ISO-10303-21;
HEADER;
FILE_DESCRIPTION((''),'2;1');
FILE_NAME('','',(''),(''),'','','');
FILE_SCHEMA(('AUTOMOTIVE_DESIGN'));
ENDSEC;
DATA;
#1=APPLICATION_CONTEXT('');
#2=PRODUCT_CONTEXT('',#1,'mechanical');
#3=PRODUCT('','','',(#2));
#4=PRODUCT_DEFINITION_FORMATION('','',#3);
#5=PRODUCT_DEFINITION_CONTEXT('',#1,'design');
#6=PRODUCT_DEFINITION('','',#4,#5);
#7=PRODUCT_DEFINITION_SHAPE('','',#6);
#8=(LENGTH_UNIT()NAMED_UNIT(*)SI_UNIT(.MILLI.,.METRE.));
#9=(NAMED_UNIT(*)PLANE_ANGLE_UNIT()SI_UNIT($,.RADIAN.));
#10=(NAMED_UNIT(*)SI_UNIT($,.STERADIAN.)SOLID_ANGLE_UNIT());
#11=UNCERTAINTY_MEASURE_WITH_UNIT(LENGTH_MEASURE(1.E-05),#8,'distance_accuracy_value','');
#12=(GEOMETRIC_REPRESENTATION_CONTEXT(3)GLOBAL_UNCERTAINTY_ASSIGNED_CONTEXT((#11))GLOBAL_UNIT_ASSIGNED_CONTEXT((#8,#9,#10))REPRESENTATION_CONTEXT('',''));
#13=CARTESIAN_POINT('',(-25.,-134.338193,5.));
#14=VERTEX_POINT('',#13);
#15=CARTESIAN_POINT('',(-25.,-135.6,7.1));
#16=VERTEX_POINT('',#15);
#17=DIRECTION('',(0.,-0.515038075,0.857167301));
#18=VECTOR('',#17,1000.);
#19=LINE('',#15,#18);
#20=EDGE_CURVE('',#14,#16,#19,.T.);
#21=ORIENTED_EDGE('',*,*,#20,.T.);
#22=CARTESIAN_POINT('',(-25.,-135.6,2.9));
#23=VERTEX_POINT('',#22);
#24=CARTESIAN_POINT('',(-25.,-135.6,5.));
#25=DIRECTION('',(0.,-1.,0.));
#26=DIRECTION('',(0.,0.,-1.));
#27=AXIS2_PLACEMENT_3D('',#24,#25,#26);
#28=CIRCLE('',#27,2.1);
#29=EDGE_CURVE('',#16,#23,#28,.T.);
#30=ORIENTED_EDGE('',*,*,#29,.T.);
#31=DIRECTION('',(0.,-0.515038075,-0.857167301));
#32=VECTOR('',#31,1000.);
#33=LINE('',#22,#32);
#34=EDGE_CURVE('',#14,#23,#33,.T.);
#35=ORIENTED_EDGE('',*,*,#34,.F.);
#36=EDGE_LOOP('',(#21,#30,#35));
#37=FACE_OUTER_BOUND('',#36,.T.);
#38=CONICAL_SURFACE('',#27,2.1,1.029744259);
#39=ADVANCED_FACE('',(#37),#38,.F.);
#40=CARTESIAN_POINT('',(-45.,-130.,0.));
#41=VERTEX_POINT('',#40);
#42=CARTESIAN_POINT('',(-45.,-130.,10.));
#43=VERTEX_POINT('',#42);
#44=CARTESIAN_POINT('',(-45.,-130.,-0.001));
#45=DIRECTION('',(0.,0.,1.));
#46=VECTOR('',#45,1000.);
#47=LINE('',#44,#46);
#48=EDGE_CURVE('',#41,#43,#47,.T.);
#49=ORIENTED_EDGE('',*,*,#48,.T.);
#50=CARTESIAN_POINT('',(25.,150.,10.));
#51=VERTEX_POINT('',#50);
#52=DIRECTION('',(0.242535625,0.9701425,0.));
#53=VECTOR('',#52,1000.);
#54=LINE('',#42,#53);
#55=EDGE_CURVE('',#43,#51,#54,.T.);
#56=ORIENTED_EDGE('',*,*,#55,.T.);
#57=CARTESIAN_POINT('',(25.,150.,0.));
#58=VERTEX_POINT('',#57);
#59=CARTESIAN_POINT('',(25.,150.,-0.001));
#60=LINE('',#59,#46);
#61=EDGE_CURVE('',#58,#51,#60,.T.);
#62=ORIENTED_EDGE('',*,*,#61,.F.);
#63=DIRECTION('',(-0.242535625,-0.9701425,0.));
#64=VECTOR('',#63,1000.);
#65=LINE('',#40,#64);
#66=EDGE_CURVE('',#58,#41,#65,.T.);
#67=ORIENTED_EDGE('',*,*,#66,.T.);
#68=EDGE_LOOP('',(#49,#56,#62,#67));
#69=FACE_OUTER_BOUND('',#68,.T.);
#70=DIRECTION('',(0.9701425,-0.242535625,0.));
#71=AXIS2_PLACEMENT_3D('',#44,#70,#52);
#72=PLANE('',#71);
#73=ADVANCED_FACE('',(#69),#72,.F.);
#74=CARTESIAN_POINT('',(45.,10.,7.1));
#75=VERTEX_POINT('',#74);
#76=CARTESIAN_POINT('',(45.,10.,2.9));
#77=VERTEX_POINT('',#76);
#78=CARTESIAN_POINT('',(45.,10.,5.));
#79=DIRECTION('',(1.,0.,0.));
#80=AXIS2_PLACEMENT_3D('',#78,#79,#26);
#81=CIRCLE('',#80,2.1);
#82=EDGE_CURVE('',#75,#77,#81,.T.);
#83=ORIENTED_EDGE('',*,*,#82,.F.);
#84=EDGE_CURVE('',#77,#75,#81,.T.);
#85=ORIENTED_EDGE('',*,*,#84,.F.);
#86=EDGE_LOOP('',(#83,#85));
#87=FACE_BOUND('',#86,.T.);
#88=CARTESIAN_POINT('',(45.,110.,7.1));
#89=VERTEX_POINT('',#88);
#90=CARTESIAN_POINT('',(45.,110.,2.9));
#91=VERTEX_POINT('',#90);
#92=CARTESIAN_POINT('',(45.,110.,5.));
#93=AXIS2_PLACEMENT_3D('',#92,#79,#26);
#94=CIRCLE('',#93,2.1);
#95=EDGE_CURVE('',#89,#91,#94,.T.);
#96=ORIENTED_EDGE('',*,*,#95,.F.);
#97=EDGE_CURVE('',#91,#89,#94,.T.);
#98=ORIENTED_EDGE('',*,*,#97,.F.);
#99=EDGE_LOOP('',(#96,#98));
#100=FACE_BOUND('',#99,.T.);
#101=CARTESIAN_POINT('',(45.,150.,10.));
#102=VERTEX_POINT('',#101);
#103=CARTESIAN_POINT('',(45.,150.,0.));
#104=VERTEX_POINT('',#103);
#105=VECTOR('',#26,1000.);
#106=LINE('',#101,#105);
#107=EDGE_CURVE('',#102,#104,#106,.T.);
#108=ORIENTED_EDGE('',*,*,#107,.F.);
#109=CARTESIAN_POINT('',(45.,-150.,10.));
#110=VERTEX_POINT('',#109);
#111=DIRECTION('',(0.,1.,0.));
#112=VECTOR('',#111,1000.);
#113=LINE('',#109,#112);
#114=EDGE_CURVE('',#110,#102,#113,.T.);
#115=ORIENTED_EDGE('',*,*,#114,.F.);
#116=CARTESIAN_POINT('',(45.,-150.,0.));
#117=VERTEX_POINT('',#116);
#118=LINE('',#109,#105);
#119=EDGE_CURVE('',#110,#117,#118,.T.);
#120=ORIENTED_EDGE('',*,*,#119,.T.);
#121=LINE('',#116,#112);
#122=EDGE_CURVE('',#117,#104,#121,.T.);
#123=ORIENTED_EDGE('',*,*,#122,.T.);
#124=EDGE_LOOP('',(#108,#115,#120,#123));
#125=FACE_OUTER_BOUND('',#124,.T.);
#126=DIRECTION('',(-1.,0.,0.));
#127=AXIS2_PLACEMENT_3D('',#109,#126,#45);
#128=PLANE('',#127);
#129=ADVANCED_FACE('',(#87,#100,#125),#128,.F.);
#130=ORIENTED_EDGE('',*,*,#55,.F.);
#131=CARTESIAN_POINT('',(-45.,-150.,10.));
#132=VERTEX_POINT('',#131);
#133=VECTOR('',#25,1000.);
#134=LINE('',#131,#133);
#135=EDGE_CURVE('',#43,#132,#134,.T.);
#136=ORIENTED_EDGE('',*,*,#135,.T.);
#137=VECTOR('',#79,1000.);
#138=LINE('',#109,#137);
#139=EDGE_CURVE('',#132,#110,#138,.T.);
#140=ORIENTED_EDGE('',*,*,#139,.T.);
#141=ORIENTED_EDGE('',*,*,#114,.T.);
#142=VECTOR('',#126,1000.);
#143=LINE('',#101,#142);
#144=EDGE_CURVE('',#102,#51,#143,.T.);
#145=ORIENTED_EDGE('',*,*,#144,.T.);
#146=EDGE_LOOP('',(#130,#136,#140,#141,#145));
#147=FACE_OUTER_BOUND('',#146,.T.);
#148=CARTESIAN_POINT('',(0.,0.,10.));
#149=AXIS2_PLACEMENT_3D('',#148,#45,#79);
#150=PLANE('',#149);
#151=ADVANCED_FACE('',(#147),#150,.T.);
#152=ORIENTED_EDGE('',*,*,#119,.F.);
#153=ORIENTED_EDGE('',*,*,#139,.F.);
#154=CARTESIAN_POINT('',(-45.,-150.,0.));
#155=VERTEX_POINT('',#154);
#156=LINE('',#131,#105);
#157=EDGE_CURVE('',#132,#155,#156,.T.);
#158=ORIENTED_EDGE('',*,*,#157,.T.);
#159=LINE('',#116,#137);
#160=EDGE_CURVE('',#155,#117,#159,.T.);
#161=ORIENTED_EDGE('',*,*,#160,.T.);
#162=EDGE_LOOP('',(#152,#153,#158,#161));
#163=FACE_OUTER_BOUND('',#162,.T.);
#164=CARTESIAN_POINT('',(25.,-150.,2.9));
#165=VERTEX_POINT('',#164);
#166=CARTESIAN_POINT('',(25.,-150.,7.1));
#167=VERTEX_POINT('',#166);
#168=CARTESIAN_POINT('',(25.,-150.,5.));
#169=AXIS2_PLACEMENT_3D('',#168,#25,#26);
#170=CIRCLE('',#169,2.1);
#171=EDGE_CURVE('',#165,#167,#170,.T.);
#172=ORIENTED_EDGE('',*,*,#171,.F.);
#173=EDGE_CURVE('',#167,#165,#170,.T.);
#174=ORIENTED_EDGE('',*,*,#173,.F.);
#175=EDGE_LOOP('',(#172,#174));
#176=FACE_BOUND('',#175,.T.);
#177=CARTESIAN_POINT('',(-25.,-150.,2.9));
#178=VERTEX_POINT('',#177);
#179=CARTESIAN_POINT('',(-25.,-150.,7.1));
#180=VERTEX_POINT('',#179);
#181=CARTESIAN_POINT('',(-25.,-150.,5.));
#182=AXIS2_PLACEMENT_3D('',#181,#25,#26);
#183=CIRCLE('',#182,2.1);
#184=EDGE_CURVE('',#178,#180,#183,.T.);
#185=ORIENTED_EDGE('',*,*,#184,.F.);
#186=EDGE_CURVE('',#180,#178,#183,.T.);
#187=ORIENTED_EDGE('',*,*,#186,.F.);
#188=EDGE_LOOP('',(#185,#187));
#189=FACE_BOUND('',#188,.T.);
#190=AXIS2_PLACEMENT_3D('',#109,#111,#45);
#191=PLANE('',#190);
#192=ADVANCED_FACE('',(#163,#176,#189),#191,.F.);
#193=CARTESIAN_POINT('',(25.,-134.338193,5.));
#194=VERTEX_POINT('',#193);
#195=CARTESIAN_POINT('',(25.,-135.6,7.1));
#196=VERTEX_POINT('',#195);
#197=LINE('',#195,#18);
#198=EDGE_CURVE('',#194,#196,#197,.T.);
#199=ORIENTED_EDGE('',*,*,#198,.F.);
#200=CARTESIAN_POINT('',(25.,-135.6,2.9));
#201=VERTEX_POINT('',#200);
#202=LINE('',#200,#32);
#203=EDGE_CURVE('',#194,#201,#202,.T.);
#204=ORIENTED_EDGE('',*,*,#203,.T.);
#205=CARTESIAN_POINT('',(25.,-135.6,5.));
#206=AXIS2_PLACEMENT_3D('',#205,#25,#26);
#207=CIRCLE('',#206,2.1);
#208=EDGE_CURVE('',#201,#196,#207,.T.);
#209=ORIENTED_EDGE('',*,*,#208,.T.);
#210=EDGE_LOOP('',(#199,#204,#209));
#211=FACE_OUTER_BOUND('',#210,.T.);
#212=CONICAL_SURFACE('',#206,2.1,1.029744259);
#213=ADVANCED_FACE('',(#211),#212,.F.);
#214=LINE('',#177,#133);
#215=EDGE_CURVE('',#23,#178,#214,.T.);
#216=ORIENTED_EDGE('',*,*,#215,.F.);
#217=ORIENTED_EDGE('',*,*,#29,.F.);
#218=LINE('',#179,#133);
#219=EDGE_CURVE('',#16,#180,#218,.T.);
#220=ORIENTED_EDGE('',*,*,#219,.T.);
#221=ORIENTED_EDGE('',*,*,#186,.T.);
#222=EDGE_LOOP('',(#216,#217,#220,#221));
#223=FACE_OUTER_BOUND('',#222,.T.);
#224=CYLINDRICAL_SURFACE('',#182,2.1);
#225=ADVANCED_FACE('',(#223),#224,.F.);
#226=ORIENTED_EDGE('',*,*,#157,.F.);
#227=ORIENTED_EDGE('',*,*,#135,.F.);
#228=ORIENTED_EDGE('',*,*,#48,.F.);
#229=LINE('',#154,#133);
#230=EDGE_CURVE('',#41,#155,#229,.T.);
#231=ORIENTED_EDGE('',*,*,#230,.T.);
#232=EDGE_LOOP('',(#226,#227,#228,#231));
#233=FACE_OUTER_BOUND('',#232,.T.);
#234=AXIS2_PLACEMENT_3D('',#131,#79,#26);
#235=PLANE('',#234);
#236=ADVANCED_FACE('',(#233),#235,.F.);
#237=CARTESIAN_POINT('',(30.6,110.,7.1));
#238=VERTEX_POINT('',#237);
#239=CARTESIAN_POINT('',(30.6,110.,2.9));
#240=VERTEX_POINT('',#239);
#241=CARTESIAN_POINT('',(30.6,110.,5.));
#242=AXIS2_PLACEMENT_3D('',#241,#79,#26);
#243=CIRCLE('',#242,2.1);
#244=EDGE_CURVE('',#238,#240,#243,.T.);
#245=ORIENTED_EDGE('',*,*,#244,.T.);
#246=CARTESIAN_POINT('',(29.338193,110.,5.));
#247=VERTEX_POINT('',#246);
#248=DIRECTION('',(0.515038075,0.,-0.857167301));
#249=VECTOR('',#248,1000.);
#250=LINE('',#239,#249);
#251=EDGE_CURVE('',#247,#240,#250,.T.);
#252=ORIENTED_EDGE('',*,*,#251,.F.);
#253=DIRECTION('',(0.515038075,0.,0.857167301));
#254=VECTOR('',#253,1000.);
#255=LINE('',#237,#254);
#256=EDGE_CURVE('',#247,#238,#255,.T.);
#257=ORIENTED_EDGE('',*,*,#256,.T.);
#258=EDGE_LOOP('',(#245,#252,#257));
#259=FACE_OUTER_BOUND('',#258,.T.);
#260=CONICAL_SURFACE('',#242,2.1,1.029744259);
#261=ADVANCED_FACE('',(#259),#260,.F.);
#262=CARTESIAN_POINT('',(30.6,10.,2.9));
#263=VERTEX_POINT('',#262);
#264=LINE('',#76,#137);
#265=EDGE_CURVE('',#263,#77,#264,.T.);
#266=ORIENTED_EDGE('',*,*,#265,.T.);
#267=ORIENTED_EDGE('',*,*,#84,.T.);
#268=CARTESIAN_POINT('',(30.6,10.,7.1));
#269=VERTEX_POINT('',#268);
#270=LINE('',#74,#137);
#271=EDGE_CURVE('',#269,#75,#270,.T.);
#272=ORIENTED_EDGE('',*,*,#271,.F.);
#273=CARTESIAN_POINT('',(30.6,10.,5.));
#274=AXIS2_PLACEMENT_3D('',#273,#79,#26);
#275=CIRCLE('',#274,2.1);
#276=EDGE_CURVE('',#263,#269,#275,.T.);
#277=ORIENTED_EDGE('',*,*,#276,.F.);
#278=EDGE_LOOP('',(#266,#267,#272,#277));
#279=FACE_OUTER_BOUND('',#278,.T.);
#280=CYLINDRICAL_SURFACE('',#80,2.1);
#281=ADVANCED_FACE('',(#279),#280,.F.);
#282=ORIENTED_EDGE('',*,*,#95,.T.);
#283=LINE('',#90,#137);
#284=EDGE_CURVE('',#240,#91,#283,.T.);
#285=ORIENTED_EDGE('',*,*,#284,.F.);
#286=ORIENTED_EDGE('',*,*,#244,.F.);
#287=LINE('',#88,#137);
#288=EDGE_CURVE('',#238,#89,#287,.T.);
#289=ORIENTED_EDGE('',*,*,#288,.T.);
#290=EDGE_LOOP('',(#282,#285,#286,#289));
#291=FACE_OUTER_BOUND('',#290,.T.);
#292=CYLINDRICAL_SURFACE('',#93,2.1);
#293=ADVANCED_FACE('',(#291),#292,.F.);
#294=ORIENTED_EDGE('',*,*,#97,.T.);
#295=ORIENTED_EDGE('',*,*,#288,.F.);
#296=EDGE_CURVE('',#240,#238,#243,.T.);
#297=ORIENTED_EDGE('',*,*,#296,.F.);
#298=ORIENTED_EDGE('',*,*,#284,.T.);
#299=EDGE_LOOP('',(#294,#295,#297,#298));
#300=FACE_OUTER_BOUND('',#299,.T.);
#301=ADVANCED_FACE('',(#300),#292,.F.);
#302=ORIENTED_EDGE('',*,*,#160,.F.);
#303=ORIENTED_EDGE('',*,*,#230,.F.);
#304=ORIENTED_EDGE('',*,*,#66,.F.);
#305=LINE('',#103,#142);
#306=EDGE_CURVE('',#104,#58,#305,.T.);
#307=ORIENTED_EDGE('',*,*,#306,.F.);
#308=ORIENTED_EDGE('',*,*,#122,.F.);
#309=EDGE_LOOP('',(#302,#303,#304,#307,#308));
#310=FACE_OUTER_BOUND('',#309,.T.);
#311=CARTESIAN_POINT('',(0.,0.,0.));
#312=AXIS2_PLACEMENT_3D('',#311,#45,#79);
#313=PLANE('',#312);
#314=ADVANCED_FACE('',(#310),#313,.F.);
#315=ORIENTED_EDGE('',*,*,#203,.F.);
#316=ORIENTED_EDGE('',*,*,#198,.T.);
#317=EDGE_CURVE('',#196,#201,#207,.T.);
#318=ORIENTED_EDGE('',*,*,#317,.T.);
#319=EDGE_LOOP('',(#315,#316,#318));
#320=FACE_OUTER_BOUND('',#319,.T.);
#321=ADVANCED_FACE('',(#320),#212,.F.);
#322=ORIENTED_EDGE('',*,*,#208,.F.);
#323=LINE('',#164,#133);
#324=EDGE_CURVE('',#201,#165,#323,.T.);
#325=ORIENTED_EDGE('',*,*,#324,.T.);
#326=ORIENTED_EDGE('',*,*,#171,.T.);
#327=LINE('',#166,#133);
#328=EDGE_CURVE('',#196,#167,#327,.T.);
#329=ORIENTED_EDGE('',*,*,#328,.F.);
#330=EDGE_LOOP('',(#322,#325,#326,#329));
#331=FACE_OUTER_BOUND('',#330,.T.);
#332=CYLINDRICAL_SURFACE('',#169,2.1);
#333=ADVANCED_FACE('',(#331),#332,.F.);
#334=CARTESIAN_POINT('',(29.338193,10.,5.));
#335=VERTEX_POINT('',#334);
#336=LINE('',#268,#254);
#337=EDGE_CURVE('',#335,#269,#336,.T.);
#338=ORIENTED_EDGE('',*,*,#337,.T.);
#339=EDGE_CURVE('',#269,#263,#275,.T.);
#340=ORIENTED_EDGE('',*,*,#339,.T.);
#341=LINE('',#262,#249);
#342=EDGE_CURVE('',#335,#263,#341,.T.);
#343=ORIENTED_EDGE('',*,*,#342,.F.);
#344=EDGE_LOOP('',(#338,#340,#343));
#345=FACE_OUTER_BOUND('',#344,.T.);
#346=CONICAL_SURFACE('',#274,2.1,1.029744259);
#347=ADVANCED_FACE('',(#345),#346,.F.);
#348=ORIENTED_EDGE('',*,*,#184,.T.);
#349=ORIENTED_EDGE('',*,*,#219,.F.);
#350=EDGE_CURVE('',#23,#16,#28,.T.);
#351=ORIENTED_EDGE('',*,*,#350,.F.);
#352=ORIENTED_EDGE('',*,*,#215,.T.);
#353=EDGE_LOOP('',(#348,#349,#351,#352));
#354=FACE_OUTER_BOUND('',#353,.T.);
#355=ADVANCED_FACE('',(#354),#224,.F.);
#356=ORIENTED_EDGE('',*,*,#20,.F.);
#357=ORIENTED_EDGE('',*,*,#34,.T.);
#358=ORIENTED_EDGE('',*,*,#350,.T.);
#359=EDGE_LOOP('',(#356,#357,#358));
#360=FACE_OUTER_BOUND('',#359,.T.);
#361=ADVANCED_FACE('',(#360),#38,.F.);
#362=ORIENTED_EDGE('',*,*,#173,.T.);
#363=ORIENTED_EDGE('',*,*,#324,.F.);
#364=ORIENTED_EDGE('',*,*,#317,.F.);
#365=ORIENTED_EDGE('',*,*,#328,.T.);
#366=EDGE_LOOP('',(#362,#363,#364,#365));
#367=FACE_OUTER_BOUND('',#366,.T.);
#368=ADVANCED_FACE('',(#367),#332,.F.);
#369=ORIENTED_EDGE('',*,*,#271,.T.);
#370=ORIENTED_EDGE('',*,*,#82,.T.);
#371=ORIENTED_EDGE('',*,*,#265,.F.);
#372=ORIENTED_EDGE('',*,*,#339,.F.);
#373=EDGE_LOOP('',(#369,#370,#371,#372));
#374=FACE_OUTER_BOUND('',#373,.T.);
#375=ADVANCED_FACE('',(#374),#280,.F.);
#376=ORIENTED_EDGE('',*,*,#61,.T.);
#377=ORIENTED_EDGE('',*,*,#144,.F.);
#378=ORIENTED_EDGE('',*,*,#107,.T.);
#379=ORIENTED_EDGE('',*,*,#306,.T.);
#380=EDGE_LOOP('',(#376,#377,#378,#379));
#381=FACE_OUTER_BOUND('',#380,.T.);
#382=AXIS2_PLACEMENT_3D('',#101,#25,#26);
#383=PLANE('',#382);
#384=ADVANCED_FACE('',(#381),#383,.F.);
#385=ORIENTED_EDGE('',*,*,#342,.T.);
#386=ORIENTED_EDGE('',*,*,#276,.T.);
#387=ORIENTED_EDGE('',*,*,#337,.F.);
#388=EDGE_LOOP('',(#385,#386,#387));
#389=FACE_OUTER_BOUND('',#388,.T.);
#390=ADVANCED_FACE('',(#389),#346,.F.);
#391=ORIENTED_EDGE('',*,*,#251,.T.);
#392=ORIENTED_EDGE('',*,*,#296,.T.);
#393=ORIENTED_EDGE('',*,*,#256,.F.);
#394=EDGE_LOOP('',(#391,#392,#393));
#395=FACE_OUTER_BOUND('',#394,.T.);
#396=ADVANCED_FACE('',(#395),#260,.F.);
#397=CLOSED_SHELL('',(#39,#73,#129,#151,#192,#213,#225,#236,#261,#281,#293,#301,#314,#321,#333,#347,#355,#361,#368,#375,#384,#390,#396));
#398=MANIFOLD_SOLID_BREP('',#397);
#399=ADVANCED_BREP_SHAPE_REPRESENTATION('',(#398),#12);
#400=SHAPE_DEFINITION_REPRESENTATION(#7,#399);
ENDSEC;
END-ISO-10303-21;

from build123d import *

# Parameters (mm, degrees)
SKETCH_1_W             = 90
SKETCH_1_H             = 300
EXTRUDE_1_DEPTH        = 10
CUT_EXTRUDE_1_REACH    = 158.924
HOLE_WIZARD_M5_1_D     = 4.2
HOLE_WIZARD_M5_1_DEPTH = 14.4
HOLE_WIZARD_M5_1_TIP   = 1.2618073
HOLE_WIZARD_M5_2_D     = 4.2
HOLE_WIZARD_M5_2_DEPTH = 14.4
HOLE_WIZARD_M5_2_TIP   = 1.2618073


with BuildPart() as part:
    # 草图1 → 凸台-拉伸1 (new body)
    with BuildSketch(Plane.XY):
        Rectangle(SKETCH_1_W, SKETCH_1_H)
    extrude(amount=EXTRUDE_1_DEPTH)

    # 草图2 → 切除-拉伸1 (cut, up to next)
    with BuildSketch(Plane.XY.offset(10), mode=Mode.PRIVATE) as cut_extrude_1_sk1:
        Polygon((25, 150), (-45, 150), (-45, -130), align=None)
    cut_extrude_1_tool1 = extrude(cut_extrude_1_sk1.sketch, amount=-CUT_EXTRUDE_1_REACH, mode=Mode.PRIVATE) & part.part
    add(cut_extrude_1_tool1.solids().sort_by_distance((-21.666667, 56.666667, 10))[0], mode=Mode.SUBTRACT)

    # M5 螺纹孔1
    with Locations(Plane(origin=(0, -150, 0), x_dir=(-1, 0, 0), z_dir=(0, -1, 0))):
        with Locations((-25, -5), (25, -5)):
            Hole(HOLE_WIZARD_M5_1_D / 2, depth=HOLE_WIZARD_M5_1_DEPTH)
            with Locations((0, 0, -(HOLE_WIZARD_M5_1_DEPTH + HOLE_WIZARD_M5_1_TIP / 2))):  # 118° drill point
                Cone(0, HOLE_WIZARD_M5_1_D / 2, HOLE_WIZARD_M5_1_TIP, mode=Mode.SUBTRACT)

    # M5 螺纹孔2
    with Locations(Plane(origin=(45, 0, 0), x_dir=(0, 0, -1), z_dir=(1, 0, 0))):
        with Locations((-5, 110), (-5, 10)):
            Hole(HOLE_WIZARD_M5_2_D / 2, depth=HOLE_WIZARD_M5_2_DEPTH)
            with Locations((0, 0, -(HOLE_WIZARD_M5_2_DEPTH + HOLE_WIZARD_M5_2_TIP / 2))):  # 118° drill point
                Cone(0, HOLE_WIZARD_M5_2_D / 2, HOLE_WIZARD_M5_2_TIP, mode=Mode.SUBTRACT)


solid = part.part
